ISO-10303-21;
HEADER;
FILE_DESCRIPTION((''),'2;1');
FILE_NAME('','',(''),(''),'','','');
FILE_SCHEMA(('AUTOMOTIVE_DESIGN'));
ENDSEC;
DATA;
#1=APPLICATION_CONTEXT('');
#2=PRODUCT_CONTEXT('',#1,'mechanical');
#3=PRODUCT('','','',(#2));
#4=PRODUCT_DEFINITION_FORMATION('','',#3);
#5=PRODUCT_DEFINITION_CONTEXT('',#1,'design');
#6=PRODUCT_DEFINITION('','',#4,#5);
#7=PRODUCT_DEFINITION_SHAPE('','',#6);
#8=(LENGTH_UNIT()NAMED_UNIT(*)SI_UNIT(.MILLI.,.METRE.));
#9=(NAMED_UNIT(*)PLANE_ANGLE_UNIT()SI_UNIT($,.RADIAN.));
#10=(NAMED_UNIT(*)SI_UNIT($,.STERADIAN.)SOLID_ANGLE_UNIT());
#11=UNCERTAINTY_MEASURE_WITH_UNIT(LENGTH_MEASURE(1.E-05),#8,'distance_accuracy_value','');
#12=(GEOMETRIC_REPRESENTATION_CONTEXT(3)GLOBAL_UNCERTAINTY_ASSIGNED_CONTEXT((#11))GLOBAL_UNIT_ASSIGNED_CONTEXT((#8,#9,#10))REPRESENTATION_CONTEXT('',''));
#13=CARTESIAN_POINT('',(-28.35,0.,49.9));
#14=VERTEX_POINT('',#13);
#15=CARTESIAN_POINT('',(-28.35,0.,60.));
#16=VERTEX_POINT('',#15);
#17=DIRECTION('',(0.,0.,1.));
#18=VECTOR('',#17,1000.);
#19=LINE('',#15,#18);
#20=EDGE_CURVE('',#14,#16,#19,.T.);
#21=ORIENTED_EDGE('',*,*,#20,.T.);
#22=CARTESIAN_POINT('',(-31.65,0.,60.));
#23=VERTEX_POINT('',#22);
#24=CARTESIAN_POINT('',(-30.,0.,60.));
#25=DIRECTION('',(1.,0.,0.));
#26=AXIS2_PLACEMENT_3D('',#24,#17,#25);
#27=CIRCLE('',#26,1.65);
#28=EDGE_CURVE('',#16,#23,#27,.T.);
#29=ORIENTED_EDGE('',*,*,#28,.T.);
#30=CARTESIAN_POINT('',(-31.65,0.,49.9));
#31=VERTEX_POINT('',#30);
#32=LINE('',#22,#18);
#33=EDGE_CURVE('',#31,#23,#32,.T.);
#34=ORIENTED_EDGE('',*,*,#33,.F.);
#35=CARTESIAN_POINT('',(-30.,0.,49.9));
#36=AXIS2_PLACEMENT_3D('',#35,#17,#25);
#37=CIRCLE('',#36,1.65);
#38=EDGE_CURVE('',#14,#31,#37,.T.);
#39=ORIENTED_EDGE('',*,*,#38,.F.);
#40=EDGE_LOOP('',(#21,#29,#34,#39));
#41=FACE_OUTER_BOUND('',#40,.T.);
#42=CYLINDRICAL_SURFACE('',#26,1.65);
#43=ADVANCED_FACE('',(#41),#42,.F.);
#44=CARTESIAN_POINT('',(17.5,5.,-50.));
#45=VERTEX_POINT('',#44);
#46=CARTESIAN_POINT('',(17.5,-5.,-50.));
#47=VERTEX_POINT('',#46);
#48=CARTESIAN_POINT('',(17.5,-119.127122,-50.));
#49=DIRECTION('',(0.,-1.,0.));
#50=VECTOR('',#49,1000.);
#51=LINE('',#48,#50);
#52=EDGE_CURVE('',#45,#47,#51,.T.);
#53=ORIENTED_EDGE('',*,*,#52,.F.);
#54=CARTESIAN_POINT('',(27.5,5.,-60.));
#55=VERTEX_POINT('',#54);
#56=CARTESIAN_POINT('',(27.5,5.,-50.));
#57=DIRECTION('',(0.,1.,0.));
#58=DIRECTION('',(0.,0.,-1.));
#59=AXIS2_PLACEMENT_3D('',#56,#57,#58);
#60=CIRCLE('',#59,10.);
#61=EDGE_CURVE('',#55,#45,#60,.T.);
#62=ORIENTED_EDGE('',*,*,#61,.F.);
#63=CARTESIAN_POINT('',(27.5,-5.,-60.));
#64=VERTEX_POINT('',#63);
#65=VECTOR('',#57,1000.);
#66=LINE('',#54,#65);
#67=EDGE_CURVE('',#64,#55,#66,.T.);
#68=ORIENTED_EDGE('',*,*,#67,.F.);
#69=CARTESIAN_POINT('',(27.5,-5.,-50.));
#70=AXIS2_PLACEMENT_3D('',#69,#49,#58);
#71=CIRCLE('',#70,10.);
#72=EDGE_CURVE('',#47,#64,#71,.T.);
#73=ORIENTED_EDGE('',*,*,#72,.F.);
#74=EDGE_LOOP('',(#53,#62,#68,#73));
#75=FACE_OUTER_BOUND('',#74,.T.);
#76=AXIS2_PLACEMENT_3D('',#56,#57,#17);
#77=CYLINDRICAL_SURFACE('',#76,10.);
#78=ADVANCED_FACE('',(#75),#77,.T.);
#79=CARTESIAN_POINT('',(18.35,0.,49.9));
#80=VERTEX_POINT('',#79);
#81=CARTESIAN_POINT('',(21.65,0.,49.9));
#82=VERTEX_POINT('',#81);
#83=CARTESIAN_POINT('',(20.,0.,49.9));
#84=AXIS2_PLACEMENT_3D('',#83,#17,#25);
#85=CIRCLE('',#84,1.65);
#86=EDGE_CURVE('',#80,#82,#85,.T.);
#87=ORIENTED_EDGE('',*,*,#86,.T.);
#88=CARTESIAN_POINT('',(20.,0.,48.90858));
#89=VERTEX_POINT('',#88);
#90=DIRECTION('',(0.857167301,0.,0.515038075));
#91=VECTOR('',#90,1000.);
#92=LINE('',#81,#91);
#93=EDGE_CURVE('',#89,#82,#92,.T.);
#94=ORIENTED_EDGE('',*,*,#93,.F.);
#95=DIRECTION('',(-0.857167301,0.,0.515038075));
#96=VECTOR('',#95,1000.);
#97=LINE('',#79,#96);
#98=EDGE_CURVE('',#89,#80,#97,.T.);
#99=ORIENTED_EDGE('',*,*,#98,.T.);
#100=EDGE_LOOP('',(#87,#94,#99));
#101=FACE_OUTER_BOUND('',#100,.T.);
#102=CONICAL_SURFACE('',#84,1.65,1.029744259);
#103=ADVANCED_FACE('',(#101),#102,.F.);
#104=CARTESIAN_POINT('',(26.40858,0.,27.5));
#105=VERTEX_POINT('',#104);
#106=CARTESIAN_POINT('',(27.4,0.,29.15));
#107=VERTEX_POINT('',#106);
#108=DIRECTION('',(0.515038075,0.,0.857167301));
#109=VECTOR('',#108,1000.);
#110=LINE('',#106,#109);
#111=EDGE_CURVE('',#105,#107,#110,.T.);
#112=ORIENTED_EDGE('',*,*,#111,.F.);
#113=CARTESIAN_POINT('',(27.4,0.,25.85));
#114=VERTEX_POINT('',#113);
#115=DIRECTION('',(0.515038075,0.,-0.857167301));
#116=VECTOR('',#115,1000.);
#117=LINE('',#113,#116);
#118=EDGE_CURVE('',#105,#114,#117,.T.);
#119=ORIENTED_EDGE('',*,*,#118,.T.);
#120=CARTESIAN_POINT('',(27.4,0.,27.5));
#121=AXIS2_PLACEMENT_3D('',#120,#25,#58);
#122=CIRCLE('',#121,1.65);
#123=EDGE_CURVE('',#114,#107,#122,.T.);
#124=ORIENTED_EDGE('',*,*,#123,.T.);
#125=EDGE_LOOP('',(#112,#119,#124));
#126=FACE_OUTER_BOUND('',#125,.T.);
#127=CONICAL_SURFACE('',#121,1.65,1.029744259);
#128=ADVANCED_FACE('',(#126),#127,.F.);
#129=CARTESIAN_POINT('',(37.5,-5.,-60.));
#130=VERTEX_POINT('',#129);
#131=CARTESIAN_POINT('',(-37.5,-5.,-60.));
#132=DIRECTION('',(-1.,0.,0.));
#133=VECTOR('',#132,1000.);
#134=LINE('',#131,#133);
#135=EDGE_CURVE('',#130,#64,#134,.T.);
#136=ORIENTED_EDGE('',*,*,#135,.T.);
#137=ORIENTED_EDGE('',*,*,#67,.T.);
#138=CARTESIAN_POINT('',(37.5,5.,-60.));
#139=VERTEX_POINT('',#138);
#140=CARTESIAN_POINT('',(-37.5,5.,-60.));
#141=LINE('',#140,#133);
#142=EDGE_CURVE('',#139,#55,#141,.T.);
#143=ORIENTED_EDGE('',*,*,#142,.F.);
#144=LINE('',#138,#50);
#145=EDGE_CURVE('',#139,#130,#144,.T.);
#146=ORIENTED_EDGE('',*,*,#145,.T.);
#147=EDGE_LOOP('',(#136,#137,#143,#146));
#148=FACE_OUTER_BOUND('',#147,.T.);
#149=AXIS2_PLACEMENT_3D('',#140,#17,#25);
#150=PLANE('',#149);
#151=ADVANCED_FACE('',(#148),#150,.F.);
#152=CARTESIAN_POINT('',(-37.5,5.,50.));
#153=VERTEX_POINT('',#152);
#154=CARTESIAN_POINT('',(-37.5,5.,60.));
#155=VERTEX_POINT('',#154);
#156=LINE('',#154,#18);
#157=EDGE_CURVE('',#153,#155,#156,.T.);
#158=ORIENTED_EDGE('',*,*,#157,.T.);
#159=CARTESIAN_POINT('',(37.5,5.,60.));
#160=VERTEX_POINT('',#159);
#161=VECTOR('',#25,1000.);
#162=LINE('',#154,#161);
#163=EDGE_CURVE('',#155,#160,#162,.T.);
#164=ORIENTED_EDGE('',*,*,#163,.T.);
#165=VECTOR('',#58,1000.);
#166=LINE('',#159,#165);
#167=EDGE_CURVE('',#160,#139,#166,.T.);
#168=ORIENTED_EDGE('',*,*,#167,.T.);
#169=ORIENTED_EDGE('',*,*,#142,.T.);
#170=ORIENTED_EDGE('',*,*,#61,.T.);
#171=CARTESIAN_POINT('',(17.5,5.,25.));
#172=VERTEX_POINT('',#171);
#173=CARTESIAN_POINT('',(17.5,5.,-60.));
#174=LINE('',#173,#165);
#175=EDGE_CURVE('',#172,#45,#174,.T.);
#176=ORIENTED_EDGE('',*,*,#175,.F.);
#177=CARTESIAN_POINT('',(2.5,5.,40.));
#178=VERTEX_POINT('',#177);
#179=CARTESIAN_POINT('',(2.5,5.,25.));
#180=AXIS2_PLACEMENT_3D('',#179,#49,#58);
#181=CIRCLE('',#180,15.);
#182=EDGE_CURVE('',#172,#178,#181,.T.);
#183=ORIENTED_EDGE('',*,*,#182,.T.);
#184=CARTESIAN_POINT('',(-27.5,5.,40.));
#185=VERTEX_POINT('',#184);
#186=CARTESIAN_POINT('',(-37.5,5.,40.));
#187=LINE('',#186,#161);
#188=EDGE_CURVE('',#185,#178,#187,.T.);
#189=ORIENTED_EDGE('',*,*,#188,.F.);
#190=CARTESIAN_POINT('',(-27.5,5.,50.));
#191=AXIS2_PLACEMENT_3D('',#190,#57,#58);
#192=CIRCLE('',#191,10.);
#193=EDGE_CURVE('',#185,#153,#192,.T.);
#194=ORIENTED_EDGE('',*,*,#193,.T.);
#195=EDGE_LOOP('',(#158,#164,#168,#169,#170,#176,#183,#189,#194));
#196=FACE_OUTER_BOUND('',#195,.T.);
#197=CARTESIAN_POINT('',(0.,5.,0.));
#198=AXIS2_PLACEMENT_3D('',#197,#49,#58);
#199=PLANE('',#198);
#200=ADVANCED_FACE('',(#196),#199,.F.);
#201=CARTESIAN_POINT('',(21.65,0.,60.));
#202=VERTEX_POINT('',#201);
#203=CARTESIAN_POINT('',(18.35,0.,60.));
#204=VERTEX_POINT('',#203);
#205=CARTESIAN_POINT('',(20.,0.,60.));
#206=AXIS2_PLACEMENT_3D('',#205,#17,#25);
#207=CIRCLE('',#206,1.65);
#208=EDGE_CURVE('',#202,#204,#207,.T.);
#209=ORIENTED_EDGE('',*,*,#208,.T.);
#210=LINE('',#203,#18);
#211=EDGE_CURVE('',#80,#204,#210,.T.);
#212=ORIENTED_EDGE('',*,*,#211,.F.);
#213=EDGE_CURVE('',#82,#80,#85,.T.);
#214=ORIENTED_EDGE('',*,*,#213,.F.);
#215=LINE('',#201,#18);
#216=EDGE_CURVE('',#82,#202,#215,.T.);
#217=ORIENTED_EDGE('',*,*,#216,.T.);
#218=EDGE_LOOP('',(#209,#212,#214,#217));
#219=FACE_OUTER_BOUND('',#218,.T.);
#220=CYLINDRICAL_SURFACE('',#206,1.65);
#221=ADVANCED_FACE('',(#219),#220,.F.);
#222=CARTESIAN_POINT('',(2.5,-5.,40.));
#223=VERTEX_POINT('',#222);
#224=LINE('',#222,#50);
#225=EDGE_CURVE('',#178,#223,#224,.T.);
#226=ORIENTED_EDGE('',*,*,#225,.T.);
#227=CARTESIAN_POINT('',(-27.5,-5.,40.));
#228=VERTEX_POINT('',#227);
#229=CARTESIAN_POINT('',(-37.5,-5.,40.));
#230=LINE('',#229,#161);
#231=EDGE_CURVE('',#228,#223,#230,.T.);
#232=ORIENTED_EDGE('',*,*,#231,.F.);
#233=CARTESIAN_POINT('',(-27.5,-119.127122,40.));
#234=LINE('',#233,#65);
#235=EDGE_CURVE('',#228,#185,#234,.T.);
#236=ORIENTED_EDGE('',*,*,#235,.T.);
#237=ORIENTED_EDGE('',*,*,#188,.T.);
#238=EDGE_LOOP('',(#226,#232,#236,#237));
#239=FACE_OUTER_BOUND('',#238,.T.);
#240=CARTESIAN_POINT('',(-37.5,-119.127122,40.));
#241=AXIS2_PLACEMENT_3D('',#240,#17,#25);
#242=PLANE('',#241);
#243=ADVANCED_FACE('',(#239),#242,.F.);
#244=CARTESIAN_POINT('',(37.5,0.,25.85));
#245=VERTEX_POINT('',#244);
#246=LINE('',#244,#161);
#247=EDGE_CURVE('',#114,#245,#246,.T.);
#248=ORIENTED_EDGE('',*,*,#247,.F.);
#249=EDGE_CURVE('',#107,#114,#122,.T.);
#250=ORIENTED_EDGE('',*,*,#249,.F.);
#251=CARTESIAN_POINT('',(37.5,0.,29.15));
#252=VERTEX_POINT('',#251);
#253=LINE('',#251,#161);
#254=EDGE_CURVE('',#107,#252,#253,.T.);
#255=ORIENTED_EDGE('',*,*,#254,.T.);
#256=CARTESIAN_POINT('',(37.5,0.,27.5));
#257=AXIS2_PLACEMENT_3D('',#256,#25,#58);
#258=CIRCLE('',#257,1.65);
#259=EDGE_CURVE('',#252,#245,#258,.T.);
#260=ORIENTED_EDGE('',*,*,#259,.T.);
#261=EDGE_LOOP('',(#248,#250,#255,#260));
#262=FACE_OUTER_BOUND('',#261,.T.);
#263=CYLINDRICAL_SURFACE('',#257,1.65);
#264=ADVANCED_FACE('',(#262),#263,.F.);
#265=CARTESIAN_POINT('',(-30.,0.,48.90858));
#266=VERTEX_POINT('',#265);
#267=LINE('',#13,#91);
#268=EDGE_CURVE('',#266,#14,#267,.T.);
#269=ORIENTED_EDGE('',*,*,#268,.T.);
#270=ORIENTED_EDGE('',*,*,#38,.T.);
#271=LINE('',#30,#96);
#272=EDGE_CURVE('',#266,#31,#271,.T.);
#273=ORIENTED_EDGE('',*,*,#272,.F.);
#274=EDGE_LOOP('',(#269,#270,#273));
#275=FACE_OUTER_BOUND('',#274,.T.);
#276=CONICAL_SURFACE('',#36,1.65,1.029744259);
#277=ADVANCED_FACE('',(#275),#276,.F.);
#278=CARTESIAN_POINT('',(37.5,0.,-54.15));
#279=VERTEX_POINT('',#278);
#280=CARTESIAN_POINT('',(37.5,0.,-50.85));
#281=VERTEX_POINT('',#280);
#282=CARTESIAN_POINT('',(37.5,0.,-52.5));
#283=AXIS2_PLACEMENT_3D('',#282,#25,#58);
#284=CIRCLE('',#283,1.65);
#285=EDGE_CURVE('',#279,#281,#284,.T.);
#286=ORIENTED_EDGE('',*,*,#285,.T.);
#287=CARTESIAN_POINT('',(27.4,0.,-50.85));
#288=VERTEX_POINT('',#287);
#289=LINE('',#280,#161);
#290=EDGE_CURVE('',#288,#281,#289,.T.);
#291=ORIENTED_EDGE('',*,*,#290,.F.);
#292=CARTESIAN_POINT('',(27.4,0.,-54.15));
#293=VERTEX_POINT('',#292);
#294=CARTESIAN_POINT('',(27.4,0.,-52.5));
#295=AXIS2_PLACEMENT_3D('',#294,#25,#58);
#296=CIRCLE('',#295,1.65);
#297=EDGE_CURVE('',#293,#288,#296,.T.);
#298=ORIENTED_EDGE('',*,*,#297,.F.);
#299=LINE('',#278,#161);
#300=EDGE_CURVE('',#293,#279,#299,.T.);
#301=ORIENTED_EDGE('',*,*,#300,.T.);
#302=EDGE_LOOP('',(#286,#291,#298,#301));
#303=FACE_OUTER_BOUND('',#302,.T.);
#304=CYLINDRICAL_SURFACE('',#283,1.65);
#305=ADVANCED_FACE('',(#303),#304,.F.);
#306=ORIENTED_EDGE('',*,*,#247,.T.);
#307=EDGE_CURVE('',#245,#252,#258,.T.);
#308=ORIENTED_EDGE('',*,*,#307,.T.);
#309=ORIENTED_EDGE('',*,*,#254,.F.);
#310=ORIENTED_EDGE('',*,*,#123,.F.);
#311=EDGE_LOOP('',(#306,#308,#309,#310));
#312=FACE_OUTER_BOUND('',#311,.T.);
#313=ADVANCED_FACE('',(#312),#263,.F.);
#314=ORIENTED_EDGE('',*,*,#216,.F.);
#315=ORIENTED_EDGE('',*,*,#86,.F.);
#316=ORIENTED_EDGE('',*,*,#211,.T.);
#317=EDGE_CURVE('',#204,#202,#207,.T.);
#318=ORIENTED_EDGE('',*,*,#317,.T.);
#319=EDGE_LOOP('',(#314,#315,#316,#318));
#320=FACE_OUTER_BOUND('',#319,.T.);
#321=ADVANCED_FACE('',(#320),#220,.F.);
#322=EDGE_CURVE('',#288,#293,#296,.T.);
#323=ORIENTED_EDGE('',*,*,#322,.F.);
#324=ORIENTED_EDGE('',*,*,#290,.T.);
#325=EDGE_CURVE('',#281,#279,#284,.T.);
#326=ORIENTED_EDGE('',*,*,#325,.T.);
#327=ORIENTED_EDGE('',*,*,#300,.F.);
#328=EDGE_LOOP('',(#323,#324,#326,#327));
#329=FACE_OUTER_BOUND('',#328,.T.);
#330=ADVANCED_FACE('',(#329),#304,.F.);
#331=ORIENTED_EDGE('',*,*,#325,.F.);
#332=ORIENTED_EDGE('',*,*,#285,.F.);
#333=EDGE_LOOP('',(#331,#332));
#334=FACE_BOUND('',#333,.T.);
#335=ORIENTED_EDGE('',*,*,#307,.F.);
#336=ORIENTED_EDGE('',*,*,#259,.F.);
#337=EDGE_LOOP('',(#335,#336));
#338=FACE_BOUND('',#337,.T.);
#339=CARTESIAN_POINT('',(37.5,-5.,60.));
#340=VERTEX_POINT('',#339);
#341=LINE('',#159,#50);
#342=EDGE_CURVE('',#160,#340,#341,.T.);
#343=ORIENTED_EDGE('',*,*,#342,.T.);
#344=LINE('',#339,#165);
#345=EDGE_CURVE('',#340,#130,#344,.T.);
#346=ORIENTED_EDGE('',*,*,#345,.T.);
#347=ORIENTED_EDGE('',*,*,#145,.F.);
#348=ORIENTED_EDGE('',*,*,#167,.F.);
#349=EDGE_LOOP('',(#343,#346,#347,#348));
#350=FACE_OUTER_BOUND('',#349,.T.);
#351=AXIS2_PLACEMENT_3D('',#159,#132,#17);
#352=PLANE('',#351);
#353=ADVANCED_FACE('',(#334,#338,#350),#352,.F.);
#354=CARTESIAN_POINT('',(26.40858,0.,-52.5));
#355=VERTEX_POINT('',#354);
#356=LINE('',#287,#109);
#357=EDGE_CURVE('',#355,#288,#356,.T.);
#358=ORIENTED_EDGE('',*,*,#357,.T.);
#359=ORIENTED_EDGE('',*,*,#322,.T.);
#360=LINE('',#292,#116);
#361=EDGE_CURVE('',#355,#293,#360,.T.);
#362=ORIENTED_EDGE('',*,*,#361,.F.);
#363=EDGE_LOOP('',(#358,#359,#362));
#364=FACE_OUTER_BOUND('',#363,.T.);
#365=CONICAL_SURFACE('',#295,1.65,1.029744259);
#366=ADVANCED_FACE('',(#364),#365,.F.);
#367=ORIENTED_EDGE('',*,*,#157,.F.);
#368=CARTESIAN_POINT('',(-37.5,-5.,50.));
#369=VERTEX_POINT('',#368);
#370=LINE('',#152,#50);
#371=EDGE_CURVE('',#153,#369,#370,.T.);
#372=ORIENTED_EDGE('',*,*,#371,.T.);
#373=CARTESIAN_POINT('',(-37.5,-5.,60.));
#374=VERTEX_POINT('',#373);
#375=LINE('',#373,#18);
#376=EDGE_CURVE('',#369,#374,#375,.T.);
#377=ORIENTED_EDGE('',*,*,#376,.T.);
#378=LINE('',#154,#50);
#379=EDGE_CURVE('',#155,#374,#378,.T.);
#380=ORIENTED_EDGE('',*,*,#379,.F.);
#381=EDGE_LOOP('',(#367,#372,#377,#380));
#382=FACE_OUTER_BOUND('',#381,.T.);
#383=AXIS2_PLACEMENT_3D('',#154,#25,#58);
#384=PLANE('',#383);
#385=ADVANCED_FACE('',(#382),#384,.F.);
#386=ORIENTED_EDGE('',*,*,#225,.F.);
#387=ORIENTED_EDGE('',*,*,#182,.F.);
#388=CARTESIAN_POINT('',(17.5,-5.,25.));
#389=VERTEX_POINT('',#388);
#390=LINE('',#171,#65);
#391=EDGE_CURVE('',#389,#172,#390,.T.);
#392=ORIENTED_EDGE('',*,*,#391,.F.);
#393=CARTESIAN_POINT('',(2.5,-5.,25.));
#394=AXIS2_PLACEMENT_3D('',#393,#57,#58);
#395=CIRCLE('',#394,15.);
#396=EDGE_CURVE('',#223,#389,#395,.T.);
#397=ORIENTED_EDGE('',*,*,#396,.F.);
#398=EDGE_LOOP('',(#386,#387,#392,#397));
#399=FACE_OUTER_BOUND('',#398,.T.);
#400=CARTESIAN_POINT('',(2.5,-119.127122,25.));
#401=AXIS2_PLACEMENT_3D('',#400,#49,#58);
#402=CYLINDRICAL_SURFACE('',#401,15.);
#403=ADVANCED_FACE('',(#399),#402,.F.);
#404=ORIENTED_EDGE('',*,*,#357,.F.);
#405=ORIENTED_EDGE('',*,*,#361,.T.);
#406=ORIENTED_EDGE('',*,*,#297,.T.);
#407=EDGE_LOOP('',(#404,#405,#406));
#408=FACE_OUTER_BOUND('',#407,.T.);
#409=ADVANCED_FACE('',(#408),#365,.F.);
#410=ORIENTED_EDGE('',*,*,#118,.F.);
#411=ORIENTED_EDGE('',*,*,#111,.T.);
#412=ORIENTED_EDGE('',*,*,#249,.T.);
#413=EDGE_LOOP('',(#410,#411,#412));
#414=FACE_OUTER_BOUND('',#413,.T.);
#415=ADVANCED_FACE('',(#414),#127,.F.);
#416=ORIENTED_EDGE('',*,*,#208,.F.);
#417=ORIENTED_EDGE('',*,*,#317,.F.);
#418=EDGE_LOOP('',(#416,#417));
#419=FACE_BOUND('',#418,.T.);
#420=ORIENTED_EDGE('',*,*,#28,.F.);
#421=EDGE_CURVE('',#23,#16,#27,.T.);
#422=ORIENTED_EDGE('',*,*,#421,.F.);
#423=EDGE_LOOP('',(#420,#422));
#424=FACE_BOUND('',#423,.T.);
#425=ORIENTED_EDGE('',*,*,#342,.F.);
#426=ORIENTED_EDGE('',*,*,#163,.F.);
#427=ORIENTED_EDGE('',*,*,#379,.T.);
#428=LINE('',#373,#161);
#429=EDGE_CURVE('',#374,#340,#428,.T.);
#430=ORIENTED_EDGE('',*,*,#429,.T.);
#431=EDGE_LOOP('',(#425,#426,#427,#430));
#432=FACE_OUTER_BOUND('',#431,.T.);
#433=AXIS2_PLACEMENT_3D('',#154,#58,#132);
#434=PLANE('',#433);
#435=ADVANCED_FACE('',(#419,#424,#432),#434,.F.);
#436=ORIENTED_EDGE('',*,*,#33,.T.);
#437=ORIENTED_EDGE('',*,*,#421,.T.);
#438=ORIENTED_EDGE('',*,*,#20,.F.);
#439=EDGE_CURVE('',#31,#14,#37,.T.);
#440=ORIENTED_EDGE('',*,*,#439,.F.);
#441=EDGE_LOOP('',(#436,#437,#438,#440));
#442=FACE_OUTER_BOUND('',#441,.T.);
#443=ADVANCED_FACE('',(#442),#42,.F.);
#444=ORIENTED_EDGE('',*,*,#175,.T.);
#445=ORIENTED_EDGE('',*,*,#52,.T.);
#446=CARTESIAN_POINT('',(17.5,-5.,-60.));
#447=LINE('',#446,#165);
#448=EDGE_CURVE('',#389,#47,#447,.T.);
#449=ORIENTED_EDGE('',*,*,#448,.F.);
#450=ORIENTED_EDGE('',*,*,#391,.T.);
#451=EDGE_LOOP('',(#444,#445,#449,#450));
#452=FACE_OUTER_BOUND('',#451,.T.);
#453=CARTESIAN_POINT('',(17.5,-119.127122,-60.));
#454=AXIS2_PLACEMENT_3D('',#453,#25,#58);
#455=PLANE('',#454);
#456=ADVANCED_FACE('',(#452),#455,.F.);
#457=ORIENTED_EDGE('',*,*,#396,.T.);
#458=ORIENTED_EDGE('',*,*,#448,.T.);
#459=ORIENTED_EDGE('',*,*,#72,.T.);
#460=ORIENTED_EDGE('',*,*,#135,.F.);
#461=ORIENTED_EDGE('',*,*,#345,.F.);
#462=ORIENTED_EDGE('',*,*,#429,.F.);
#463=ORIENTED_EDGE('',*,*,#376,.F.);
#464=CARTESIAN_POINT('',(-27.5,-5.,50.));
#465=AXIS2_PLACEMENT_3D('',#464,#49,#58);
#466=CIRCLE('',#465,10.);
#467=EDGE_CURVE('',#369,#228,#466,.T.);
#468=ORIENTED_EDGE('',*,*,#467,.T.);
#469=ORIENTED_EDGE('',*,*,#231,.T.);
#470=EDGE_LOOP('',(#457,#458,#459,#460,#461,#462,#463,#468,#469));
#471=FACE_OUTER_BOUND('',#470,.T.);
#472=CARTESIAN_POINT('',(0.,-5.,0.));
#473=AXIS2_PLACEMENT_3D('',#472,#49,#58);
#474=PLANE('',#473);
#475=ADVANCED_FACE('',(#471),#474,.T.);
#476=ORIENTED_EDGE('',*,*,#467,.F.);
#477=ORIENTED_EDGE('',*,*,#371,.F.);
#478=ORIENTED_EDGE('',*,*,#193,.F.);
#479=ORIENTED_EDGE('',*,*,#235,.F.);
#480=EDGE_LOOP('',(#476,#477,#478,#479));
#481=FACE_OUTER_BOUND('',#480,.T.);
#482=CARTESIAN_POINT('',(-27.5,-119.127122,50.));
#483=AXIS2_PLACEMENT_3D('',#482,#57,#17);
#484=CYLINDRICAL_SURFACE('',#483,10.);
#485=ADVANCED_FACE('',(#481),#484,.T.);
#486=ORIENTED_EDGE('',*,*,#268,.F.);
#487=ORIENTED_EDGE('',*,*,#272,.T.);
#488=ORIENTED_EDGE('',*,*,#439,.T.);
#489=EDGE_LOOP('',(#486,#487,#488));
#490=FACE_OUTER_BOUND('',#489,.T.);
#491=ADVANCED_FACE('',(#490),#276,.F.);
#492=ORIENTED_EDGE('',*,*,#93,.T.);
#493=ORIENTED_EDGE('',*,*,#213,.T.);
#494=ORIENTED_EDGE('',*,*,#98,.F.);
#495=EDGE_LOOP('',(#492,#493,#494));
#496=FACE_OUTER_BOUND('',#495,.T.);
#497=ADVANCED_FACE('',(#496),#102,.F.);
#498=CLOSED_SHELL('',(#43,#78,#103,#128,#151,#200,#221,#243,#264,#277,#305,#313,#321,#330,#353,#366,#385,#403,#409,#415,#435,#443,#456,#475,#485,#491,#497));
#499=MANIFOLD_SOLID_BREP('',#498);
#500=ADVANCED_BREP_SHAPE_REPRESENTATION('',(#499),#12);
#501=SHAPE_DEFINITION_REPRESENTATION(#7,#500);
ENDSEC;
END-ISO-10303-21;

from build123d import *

# Parameters (mm, degrees)
SKETCH_1_W             = 75
SKETCH_1_H             = 120
EXTRUDE_1_DEPTH        = 5
SKETCH_2_W             = 55
SKETCH_2_H             = 100
CUT_EXTRUDE_1_DEPTH    = 10
FILLET_1_R             = 15
FILLET_2_R             = 10
HOLE_WIZARD_M4_1_D     = 3.3
HOLE_WIZARD_M4_1_DEPTH = 10.1
HOLE_WIZARD_M4_1_TIP   = 0.991420021
HOLE_WIZARD_M4_2_D     = 3.3
HOLE_WIZARD_M4_2_DEPTH = 10.1
HOLE_WIZARD_M4_2_TIP   = 0.991420021


with BuildPart() as part:
    # 草图1 → 凸台-拉伸1 (new, symmetric)
    with BuildSketch(Plane(origin=(0, 0, 0), x_dir=(1, 0, 0), z_dir=(0, 1, 0))):
        Rectangle(SKETCH_1_W, SKETCH_1_H)
    extrude(amount=EXTRUDE_1_DEPTH, both=True)

    # 草图2 → 切除-拉伸1 (cut)
    with BuildSketch(Plane(origin=(0, 5, 0), x_dir=(1, 0, 0), z_dir=(0, 1, 0))):
        with Locations((-10, 10)):
            Rectangle(SKETCH_2_W, SKETCH_2_H)
    extrude(amount=-CUT_EXTRUDE_1_DEPTH, mode=Mode.SUBTRACT)

    # 圆角1
    fillet_1_edges = [part.edges().sort_by_distance(p)[0] for p in [
        (17.5, 0, 40),
    ]]
    fillet(fillet_1_edges, radius=FILLET_1_R)

    # 圆角2
    fillet_2_edges = [part.edges().sort_by_distance(p)[0] for p in [
        (17.5, 0, -60),
        (-37.5, 0, 40),
    ]]
    fillet(fillet_2_edges, radius=FILLET_2_R)

    # M4 螺纹孔1
    with Locations(Plane.XY.offset(60)):
        with Locations((-30, 0), (20, 0)):
            Hole(HOLE_WIZARD_M4_1_D / 2, depth=HOLE_WIZARD_M4_1_DEPTH)
            with Locations((0, 0, -(HOLE_WIZARD_M4_1_DEPTH + HOLE_WIZARD_M4_1_TIP / 2))):  # 118° drill point
                Cone(0, HOLE_WIZARD_M4_1_D / 2, HOLE_WIZARD_M4_1_TIP, mode=Mode.SUBTRACT)

    # M4 螺纹孔2
    with Locations(Plane(origin=(37.5, 0, 0), x_dir=(0, 0, -1), z_dir=(1, 0, 0))):
        with Locations((-27.5, 0), (52.5, 0)):
            Hole(HOLE_WIZARD_M4_2_D / 2, depth=HOLE_WIZARD_M4_2_DEPTH)
            with Locations((0, 0, -(HOLE_WIZARD_M4_2_DEPTH + HOLE_WIZARD_M4_2_TIP / 2))):  # 118° drill point
                Cone(0, HOLE_WIZARD_M4_2_D / 2, HOLE_WIZARD_M4_2_TIP, mode=Mode.SUBTRACT)


solid = part.part
